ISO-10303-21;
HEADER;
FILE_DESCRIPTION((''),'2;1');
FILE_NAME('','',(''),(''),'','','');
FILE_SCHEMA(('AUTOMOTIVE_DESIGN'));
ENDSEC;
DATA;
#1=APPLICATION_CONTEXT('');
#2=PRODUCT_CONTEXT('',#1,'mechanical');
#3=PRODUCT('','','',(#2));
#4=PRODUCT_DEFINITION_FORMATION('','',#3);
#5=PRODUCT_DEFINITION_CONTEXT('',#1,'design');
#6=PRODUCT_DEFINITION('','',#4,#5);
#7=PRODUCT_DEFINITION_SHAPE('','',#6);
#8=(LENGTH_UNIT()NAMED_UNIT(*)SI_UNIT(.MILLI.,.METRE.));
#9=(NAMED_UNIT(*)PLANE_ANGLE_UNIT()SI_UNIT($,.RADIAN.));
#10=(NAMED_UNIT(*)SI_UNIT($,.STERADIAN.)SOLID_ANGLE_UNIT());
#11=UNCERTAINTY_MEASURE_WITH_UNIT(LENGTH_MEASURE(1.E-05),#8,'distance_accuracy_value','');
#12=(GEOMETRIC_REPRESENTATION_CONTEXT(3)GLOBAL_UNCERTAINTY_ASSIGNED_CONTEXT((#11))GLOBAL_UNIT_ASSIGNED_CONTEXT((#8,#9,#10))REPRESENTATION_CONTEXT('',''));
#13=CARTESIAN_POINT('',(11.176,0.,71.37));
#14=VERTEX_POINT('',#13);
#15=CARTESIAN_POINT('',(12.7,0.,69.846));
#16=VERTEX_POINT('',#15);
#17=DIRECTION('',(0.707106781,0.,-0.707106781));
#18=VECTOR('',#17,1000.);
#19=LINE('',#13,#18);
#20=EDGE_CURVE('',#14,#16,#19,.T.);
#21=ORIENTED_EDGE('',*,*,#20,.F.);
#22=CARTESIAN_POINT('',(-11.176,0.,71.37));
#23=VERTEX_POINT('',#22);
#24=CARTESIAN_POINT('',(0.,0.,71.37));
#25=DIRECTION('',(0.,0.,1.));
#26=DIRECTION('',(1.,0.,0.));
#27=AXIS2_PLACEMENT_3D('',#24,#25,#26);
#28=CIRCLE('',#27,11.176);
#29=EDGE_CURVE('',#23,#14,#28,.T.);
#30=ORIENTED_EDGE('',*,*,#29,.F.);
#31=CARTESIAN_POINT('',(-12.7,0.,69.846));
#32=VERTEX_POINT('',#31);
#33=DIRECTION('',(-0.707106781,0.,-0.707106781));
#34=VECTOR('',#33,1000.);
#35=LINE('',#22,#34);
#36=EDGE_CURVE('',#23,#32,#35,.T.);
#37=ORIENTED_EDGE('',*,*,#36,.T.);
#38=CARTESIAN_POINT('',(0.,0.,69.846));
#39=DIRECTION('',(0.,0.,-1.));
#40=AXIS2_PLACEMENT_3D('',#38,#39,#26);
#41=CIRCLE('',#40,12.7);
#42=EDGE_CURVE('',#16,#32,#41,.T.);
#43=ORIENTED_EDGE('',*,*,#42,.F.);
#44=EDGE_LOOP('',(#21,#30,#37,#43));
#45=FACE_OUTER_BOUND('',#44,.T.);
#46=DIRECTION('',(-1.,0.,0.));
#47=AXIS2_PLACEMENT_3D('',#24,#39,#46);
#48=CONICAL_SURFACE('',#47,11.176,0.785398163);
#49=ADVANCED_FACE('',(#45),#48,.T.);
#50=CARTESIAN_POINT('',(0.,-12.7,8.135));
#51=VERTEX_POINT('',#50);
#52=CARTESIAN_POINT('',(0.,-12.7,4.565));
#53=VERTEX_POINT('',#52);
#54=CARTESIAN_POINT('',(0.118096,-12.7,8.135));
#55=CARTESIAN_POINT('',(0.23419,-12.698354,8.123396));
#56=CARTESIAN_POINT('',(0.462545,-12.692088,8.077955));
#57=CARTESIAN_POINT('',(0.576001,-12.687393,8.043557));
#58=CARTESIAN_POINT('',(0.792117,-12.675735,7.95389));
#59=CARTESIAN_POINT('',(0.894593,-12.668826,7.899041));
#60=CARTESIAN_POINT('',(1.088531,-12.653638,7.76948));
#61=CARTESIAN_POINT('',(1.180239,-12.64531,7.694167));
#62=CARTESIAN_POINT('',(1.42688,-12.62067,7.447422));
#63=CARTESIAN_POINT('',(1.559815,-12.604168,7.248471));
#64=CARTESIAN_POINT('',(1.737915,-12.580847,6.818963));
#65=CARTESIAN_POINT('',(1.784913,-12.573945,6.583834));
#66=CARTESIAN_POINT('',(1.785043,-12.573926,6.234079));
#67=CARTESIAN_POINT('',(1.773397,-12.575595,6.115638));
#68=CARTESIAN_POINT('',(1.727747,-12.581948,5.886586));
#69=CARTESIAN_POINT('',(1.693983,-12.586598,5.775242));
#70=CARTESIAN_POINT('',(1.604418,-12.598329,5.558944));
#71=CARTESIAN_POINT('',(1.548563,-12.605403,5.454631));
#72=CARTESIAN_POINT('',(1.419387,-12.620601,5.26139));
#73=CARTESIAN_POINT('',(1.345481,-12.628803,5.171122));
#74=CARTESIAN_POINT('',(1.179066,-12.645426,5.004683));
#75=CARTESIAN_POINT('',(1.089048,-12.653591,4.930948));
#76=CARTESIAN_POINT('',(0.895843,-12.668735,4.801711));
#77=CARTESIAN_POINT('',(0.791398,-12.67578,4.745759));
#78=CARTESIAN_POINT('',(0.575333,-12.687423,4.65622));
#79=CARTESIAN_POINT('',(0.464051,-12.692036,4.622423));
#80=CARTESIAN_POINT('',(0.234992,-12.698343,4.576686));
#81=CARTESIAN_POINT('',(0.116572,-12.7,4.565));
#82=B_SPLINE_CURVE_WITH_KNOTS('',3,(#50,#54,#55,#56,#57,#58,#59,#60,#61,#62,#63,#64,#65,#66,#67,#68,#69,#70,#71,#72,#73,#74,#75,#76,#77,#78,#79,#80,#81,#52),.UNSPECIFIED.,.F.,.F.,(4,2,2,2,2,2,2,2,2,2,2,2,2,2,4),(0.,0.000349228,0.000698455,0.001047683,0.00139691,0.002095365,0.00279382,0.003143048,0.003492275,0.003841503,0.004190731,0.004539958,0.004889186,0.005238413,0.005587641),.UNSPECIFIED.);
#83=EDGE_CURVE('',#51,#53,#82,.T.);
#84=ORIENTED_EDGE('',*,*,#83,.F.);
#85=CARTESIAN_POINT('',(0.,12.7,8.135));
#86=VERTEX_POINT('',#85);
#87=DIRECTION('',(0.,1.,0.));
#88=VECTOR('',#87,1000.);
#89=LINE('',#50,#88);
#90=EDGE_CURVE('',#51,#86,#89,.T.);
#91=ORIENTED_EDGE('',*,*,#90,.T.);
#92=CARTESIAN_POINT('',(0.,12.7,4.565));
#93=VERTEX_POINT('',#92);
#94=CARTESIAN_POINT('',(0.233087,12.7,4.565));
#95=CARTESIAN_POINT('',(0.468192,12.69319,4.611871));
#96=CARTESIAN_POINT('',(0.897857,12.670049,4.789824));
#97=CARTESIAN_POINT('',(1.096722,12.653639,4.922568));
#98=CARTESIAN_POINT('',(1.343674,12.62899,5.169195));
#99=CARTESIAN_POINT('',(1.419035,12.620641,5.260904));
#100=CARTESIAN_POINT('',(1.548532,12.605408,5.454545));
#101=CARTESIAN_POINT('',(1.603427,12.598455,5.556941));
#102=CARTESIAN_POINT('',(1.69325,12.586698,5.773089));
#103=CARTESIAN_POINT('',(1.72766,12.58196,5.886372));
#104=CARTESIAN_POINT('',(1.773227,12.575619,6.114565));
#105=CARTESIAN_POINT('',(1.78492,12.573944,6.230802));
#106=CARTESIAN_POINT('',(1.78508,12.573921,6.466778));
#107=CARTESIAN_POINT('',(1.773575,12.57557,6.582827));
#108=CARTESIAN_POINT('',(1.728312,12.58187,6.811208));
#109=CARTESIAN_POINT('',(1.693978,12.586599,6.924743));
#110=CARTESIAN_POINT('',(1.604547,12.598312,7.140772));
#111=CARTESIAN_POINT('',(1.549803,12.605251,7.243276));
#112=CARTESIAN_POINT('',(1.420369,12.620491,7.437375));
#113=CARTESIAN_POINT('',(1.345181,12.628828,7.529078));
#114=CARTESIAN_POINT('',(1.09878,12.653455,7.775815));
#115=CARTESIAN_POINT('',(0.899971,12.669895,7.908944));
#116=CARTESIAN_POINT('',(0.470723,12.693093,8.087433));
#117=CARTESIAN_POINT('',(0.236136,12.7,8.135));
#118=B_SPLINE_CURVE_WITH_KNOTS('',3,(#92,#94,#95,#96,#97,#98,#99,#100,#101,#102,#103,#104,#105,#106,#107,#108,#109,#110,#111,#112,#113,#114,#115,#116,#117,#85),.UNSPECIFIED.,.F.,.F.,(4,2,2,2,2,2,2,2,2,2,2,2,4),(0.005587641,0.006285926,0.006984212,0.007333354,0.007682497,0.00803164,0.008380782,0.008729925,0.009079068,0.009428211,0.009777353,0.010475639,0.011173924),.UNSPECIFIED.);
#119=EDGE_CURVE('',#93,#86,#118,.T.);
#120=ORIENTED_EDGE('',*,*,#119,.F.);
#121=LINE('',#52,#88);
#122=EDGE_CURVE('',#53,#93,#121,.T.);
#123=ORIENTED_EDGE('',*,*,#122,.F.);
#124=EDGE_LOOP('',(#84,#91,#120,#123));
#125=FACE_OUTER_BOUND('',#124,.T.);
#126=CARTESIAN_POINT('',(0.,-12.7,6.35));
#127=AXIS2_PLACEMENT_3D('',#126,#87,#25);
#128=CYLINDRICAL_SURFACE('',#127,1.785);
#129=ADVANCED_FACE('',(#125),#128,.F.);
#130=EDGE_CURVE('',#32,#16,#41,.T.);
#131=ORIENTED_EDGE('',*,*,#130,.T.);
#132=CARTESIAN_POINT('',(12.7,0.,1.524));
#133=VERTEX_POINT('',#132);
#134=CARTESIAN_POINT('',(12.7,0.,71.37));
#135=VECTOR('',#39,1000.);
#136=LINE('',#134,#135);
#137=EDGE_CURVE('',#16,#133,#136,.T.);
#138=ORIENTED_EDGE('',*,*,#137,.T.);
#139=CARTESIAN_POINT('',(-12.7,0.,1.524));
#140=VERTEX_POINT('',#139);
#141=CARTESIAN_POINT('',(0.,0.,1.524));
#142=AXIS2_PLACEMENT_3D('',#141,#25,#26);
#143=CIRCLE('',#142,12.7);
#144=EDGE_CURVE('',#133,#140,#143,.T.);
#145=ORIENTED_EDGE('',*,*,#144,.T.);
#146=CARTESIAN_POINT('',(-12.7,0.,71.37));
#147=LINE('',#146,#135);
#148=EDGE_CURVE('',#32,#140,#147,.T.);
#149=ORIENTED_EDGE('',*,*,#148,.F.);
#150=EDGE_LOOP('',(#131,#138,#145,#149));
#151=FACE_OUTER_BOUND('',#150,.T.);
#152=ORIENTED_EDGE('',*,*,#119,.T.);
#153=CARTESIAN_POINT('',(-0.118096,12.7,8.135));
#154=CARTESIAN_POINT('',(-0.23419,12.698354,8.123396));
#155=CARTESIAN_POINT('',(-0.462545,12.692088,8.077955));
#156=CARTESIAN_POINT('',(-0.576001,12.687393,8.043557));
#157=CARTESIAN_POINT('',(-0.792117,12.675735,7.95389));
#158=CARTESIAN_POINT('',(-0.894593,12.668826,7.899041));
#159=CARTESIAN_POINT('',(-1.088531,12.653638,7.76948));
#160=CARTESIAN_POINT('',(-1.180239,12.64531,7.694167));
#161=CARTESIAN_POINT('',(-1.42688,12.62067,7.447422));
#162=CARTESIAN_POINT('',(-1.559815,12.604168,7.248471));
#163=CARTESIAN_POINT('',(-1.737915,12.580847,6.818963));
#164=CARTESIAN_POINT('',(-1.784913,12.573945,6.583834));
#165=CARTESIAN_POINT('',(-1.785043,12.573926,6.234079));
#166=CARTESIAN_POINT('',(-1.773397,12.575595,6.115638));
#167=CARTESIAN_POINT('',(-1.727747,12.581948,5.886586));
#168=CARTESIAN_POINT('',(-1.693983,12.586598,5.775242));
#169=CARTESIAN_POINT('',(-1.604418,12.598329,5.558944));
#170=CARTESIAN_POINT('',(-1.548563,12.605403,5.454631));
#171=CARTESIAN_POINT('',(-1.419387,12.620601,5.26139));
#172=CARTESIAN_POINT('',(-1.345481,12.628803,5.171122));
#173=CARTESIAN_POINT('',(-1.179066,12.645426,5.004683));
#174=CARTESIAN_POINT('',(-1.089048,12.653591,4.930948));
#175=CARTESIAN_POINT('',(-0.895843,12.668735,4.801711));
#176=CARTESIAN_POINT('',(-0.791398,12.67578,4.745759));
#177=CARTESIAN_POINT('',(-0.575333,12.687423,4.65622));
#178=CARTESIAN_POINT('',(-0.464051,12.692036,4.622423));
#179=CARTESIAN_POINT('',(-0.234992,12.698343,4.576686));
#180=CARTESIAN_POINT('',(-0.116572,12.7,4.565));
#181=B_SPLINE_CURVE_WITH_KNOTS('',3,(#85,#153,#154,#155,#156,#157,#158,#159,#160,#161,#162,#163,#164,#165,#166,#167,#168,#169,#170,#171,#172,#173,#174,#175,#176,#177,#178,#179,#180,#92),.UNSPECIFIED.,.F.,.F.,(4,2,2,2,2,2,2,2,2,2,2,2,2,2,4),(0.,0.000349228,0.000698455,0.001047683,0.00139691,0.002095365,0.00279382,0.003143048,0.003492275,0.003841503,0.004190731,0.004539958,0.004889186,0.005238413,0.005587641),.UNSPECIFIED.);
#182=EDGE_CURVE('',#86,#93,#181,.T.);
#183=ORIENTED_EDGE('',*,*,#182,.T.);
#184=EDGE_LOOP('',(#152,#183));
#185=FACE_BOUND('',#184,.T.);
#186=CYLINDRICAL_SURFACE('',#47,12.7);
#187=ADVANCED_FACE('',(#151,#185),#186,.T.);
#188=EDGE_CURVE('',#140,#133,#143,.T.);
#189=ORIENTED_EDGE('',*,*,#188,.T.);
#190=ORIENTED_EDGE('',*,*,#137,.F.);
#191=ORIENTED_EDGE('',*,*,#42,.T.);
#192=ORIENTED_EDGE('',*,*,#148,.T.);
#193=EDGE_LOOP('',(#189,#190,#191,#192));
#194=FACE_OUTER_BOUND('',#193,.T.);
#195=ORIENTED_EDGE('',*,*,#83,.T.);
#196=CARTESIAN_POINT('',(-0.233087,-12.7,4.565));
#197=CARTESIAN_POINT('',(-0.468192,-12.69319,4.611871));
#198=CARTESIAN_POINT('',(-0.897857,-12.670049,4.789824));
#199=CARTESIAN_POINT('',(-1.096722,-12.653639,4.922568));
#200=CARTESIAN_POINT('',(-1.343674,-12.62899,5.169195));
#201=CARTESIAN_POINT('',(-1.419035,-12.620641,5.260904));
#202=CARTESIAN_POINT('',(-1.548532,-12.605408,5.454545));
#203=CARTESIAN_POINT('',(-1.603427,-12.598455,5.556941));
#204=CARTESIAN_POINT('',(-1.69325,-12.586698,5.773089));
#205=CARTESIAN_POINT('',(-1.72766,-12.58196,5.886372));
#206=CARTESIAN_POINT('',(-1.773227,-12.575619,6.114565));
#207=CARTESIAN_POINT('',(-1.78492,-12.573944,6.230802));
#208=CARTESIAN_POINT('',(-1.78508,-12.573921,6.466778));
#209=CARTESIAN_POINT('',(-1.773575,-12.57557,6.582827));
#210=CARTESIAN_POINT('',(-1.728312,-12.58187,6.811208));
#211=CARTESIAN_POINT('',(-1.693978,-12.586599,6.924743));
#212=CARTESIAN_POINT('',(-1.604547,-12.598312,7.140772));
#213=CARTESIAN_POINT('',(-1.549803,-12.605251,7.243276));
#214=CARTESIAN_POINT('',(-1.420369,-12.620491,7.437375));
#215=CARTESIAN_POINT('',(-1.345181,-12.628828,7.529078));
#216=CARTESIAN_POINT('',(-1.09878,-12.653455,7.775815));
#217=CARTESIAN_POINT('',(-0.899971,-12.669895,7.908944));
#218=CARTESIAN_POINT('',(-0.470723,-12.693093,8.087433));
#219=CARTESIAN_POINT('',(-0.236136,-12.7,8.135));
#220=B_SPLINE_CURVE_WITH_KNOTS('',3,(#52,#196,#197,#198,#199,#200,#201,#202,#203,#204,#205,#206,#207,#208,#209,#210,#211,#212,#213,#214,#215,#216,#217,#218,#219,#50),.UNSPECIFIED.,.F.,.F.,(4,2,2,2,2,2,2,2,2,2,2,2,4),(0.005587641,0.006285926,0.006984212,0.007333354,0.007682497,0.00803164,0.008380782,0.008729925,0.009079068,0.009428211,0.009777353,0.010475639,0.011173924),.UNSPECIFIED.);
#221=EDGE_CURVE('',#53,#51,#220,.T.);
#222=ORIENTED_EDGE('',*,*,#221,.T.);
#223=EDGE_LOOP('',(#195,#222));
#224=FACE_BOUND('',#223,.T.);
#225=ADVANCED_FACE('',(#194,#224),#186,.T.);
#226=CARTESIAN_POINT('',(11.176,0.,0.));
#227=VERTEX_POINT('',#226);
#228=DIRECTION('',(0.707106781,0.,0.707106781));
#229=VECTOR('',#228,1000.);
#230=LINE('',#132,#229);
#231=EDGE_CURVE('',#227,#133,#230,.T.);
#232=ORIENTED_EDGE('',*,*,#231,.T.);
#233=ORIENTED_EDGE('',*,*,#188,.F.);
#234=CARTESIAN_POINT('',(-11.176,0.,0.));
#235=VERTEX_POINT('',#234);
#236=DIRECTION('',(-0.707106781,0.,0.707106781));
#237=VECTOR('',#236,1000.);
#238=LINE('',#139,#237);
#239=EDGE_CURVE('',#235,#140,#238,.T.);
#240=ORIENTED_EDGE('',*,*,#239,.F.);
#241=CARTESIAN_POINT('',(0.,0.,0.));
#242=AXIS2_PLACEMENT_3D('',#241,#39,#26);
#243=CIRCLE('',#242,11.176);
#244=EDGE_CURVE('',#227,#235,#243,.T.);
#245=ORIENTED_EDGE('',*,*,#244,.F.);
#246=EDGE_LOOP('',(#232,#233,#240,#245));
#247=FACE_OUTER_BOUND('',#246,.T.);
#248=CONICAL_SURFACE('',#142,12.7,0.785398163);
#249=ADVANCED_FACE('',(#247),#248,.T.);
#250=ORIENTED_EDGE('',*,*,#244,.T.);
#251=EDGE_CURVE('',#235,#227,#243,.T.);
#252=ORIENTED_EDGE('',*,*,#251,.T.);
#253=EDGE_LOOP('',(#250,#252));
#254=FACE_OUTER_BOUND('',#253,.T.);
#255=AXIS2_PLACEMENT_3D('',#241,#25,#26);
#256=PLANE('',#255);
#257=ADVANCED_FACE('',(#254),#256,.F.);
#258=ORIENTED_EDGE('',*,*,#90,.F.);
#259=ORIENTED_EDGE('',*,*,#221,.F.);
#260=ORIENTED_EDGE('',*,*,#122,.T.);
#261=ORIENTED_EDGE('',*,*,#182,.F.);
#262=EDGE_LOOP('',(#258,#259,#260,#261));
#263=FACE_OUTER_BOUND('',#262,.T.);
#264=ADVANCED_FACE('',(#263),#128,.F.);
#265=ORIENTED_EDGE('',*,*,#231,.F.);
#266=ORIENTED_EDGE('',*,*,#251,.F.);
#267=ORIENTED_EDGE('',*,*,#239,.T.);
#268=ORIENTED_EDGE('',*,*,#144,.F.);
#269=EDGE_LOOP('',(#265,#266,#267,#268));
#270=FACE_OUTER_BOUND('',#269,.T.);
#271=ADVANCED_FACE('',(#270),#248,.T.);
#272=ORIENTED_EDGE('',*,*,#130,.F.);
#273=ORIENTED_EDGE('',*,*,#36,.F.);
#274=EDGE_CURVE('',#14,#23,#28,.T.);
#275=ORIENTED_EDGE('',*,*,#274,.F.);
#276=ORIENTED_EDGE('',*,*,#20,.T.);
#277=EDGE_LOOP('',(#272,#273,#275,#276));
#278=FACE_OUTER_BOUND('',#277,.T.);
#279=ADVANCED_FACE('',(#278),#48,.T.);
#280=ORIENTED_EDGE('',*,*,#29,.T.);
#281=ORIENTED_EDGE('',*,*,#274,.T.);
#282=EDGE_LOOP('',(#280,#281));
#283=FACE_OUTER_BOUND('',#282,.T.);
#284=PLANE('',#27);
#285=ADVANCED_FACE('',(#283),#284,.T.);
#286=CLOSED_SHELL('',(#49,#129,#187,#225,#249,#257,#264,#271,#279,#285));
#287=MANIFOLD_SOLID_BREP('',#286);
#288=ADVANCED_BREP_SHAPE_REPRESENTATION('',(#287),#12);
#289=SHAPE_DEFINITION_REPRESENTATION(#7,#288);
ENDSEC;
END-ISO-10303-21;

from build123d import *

# Parameters (mm, degrees)
SKETCH1_R               = 12.7
BOSS_EXTRUDE1_DEPTH     = 71.37
CHAMFER1_SIZE           = 1.524
CUT_EXTRUDE1_DEPTH      = 74.59522335
CUT_EXTRUDE1_DEPTH_BACK = 74.59522335
SKETCH2_R               = 1.785


with BuildPart() as part:
    # Sketch1 → Boss-Extrude1 (new body)
    with BuildSketch(Plane.XY):
        Circle(SKETCH1_R)
    extrude(amount=BOSS_EXTRUDE1_DEPTH)

    # Chamfer1
    chamfer1_edges = [part.edges().sort_by_distance(p)[0] for p in [
        (-12.7, 0, 0),
        (-12.7, 0, 71.37),
    ]]
    chamfer(chamfer1_edges, length=CHAMFER1_SIZE)

    # Sketch2 → Cut-Extrude1 (cut, two sides: drawn at the far end of the back side and taken through both)
    with BuildSketch(Plane(origin=(0, 0, 0), x_dir=(1, 0, 0), z_dir=(0, 1, 0)).offset(-CUT_EXTRUDE1_DEPTH_BACK)):
        with Locations(Location((0, -6.35, 0), (0, 0, 270))):
            Circle(SKETCH2_R)
    extrude(amount=CUT_EXTRUDE1_DEPTH + CUT_EXTRUDE1_DEPTH_BACK, mode=Mode.SUBTRACT)


solid = part.part
